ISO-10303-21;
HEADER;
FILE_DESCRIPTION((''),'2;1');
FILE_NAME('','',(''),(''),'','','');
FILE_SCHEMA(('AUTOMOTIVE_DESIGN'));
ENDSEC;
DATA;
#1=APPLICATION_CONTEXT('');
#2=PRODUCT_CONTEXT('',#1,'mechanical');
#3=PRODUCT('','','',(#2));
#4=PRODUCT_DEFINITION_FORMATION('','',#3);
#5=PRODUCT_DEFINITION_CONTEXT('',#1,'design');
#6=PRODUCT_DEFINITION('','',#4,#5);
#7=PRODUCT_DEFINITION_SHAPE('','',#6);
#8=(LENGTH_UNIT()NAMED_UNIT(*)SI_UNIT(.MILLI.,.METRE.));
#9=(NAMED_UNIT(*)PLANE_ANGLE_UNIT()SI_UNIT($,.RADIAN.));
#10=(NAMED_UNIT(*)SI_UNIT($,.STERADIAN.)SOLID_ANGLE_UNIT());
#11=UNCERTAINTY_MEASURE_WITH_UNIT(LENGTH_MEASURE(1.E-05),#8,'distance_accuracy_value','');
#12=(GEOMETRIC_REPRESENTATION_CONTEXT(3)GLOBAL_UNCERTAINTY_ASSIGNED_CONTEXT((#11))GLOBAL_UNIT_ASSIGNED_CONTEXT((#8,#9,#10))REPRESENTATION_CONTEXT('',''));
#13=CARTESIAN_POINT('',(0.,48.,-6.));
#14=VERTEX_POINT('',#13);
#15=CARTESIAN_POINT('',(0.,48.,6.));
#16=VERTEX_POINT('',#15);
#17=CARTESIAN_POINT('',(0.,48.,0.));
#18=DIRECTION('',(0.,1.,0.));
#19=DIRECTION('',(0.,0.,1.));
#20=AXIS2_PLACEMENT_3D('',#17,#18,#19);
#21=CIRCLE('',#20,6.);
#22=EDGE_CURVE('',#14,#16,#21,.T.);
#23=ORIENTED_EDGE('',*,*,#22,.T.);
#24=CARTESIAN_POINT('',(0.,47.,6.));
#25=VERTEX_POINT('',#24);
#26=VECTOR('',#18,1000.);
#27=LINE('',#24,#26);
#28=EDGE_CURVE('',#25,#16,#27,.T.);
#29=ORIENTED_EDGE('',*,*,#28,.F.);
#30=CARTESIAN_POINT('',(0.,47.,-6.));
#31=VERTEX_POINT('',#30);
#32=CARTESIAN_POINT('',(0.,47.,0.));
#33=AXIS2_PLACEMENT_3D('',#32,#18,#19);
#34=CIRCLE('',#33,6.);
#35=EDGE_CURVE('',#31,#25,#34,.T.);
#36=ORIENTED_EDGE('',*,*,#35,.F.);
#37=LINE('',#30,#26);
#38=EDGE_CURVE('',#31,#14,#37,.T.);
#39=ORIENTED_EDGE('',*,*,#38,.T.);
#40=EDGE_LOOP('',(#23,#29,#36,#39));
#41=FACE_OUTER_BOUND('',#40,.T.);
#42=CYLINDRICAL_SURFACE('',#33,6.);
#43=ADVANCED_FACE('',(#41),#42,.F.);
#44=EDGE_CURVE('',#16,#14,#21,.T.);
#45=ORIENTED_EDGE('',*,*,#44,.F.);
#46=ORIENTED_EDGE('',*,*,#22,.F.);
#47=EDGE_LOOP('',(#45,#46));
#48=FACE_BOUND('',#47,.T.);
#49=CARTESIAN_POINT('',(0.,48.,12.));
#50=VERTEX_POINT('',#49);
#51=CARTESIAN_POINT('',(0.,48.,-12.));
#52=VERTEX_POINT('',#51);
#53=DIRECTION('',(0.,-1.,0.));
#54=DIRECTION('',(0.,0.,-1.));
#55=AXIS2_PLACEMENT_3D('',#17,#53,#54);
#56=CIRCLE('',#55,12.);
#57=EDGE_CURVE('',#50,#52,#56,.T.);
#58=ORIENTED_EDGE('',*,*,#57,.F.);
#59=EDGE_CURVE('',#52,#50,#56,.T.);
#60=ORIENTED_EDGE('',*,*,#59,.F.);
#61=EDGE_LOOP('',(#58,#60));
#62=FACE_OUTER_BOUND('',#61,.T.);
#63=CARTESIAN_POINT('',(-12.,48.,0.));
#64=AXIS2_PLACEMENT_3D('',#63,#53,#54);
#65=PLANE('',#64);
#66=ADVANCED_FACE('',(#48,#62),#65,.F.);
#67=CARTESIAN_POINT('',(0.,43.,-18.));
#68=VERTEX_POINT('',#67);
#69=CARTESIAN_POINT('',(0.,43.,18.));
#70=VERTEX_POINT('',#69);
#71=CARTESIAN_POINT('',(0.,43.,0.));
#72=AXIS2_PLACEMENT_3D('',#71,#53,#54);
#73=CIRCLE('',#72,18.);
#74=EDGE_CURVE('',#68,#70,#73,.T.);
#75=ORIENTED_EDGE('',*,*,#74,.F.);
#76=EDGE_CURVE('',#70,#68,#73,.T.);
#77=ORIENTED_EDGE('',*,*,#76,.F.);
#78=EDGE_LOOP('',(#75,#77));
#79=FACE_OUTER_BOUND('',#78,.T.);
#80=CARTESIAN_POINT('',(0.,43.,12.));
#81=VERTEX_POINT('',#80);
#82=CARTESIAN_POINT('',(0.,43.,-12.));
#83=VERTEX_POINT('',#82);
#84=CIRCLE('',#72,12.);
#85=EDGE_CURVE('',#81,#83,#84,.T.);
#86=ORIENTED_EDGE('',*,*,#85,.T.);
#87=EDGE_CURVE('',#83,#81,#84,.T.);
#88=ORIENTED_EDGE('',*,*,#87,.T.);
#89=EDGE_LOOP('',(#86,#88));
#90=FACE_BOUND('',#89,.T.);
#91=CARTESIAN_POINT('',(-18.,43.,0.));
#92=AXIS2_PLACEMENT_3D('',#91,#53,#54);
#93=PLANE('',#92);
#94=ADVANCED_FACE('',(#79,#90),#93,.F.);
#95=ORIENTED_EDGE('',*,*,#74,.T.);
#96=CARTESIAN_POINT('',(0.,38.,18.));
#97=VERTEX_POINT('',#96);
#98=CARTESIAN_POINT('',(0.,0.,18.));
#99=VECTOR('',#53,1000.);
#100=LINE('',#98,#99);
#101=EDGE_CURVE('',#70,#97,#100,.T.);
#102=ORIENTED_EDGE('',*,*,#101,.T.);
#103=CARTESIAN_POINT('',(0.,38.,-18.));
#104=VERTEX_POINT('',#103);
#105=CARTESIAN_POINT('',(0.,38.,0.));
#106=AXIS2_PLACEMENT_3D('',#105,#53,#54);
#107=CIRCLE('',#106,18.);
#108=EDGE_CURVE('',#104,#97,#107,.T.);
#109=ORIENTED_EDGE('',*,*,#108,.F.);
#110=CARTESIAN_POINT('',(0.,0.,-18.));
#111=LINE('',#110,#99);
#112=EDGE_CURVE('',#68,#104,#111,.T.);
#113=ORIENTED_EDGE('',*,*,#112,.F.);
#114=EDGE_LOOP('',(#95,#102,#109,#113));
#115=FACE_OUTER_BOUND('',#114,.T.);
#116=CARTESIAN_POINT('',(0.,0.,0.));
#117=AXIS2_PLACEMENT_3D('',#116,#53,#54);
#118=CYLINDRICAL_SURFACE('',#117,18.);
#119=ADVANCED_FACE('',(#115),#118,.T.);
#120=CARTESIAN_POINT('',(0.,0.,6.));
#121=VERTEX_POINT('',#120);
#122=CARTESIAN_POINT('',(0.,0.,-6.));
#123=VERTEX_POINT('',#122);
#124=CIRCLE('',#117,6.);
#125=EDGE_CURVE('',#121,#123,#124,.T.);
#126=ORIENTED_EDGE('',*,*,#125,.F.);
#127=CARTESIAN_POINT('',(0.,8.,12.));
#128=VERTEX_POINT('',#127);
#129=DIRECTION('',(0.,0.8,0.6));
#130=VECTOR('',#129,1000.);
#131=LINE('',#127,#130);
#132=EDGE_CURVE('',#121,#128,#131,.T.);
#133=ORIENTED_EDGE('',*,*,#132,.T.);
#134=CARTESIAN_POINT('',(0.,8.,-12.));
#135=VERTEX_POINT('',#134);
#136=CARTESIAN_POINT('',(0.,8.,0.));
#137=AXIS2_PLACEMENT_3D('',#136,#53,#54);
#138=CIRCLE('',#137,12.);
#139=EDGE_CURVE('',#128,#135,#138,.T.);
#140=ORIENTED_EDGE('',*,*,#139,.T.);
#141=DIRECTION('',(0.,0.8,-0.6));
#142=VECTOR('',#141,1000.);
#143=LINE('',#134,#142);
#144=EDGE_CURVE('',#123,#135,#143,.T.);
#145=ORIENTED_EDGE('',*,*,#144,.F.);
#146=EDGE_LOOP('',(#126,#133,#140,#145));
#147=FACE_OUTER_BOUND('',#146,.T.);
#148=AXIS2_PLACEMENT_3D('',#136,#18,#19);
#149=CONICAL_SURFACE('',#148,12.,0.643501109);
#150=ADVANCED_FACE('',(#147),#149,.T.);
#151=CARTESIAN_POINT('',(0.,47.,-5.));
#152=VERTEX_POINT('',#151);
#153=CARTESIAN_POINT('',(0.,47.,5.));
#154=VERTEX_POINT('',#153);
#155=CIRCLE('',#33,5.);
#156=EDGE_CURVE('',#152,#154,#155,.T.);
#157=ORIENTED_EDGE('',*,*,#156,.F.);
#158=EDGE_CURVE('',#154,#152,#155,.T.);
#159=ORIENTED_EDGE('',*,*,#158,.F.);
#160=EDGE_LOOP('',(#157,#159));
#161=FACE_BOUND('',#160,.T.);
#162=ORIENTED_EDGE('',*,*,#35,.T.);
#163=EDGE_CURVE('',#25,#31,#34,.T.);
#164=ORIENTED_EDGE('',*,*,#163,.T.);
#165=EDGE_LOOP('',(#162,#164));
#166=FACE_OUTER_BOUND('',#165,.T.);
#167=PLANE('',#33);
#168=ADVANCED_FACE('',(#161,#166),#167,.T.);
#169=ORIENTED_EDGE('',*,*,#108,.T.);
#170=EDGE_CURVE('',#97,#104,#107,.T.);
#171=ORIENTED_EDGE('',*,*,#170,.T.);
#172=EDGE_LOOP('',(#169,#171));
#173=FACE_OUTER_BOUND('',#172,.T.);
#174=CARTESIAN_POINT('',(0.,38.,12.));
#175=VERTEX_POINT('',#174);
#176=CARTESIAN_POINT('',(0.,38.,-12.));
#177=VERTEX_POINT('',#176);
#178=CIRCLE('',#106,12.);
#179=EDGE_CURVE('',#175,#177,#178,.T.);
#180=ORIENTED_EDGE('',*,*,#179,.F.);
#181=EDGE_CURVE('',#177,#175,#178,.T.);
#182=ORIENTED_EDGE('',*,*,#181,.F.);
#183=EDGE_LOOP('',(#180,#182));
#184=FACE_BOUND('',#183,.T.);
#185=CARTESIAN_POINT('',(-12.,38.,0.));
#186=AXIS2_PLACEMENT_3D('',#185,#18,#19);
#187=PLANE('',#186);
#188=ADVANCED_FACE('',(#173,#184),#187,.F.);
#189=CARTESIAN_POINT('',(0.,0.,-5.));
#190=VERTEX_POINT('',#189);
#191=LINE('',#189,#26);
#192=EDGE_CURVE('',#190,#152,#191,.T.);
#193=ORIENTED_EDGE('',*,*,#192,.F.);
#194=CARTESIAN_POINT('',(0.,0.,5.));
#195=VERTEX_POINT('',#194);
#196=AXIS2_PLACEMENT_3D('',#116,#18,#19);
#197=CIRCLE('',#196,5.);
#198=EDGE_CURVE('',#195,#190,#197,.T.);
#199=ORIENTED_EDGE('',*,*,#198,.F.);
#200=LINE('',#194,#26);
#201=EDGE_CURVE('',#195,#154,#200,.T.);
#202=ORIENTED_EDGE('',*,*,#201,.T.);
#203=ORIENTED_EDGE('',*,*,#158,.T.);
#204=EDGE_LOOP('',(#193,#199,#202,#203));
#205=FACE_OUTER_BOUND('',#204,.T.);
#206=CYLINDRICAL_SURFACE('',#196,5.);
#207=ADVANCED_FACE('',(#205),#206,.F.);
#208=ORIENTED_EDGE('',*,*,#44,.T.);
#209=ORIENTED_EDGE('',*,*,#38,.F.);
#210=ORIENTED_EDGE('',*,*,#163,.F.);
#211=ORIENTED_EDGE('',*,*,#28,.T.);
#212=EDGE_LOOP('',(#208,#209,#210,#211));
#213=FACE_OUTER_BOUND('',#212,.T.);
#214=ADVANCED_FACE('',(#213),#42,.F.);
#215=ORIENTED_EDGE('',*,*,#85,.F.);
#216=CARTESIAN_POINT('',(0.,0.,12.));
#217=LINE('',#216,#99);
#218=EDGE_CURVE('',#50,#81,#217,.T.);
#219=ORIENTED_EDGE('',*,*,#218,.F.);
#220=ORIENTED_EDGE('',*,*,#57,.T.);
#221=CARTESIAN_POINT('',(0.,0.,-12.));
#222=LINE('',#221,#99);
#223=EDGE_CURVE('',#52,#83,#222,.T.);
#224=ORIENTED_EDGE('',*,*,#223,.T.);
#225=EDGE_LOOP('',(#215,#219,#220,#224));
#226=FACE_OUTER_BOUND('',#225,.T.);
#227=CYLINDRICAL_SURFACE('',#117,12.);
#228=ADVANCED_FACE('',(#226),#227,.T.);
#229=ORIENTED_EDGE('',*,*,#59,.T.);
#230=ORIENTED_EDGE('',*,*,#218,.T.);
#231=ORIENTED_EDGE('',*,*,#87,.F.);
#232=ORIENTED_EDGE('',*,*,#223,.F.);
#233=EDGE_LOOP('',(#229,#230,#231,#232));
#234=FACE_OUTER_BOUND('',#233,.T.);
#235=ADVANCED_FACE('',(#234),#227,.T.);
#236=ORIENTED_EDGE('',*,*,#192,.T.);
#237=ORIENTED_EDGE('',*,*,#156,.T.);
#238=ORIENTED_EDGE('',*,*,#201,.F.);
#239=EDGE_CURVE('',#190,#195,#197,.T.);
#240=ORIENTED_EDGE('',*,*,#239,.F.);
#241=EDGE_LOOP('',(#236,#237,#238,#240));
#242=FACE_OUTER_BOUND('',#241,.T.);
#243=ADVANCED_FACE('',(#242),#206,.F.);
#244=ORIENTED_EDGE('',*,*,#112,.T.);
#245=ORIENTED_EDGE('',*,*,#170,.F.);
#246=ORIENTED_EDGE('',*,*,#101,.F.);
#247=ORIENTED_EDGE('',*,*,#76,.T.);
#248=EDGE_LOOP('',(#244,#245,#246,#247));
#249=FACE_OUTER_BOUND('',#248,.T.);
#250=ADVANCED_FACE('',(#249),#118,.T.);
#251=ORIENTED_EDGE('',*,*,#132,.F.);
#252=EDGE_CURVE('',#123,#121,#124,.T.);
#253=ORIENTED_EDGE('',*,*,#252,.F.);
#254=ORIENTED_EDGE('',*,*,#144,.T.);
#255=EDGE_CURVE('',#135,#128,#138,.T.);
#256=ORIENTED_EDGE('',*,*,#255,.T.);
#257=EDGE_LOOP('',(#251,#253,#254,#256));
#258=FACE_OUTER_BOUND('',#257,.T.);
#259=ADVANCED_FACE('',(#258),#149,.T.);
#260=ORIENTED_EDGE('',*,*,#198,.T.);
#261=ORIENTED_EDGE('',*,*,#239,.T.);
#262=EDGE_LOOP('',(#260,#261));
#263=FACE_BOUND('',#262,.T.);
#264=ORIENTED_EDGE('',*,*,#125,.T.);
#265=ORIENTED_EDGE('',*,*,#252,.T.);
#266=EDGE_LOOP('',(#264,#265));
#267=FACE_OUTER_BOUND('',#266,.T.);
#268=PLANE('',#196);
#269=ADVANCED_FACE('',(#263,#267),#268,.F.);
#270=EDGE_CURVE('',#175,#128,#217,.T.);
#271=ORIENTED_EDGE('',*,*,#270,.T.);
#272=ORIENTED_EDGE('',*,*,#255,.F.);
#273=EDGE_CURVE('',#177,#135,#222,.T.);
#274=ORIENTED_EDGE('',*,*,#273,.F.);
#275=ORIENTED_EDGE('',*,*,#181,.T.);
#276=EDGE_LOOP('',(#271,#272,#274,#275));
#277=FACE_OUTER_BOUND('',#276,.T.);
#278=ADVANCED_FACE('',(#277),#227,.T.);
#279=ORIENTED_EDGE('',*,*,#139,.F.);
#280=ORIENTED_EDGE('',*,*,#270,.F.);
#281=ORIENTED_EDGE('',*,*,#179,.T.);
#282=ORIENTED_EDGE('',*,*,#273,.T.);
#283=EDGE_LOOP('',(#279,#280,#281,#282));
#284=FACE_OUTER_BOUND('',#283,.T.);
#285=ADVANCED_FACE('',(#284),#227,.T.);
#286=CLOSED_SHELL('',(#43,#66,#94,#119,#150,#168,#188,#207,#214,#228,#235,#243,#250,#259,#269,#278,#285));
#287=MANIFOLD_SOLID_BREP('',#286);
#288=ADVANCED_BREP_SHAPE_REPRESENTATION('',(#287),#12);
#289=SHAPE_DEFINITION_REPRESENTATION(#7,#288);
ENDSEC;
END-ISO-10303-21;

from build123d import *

# Parameters (mm, degrees)
COUNTERBORE_SKETCH_12_R = 6
COUNTERBORE_12X1_DEPTH  = 1
BORE_SKETCH_10_R        = 5
BORE_10X47_DEPTH        = 47


with BuildPart() as part:
    # Nozzle Profile Sketch → Nozzle Body Revolve (revolve)
    with BuildSketch(Plane.XY, mode=Mode.PRIVATE) as nozzle_body_revolve_sk:
        Polygon((0, 0), (0, 48), (-12, 48), (-12, 43), (-18, 43), (-18, 38), (-12, 38), (-12, 8), (-6, 0), align=None)
    revolve(nozzle_body_revolve_sk.sketch.rotate(Axis((0, 0, 0), (0, 1, 0)), 270), axis=Axis((0, 0, 0), (0, 1, 0)))

    # Counterbore Sketch Ø12 → Counterbore Ø12x1 (cut)
    with BuildSketch(Plane(origin=(0, 48, 0), x_dir=(1, 0, 0), z_dir=(0, 1, 0))):
        with Locations(Location((0, 0, 0), (0, 0, 270))):
            Circle(COUNTERBORE_SKETCH_12_R)
    extrude(amount=-COUNTERBORE_12X1_DEPTH, mode=Mode.SUBTRACT)

    # Bore Sketch Ø10 → Bore Ø10x47 (cut)
    with BuildSketch(Plane(origin=(0, 47, 0), x_dir=(1, 0, 0), z_dir=(0, 1, 0))):
        with Locations(Location((0, 0, 0), (0, 0, 270))):
            Circle(BORE_SKETCH_10_R)
    extrude(amount=-BORE_10X47_DEPTH, mode=Mode.SUBTRACT)


solid = part.part
